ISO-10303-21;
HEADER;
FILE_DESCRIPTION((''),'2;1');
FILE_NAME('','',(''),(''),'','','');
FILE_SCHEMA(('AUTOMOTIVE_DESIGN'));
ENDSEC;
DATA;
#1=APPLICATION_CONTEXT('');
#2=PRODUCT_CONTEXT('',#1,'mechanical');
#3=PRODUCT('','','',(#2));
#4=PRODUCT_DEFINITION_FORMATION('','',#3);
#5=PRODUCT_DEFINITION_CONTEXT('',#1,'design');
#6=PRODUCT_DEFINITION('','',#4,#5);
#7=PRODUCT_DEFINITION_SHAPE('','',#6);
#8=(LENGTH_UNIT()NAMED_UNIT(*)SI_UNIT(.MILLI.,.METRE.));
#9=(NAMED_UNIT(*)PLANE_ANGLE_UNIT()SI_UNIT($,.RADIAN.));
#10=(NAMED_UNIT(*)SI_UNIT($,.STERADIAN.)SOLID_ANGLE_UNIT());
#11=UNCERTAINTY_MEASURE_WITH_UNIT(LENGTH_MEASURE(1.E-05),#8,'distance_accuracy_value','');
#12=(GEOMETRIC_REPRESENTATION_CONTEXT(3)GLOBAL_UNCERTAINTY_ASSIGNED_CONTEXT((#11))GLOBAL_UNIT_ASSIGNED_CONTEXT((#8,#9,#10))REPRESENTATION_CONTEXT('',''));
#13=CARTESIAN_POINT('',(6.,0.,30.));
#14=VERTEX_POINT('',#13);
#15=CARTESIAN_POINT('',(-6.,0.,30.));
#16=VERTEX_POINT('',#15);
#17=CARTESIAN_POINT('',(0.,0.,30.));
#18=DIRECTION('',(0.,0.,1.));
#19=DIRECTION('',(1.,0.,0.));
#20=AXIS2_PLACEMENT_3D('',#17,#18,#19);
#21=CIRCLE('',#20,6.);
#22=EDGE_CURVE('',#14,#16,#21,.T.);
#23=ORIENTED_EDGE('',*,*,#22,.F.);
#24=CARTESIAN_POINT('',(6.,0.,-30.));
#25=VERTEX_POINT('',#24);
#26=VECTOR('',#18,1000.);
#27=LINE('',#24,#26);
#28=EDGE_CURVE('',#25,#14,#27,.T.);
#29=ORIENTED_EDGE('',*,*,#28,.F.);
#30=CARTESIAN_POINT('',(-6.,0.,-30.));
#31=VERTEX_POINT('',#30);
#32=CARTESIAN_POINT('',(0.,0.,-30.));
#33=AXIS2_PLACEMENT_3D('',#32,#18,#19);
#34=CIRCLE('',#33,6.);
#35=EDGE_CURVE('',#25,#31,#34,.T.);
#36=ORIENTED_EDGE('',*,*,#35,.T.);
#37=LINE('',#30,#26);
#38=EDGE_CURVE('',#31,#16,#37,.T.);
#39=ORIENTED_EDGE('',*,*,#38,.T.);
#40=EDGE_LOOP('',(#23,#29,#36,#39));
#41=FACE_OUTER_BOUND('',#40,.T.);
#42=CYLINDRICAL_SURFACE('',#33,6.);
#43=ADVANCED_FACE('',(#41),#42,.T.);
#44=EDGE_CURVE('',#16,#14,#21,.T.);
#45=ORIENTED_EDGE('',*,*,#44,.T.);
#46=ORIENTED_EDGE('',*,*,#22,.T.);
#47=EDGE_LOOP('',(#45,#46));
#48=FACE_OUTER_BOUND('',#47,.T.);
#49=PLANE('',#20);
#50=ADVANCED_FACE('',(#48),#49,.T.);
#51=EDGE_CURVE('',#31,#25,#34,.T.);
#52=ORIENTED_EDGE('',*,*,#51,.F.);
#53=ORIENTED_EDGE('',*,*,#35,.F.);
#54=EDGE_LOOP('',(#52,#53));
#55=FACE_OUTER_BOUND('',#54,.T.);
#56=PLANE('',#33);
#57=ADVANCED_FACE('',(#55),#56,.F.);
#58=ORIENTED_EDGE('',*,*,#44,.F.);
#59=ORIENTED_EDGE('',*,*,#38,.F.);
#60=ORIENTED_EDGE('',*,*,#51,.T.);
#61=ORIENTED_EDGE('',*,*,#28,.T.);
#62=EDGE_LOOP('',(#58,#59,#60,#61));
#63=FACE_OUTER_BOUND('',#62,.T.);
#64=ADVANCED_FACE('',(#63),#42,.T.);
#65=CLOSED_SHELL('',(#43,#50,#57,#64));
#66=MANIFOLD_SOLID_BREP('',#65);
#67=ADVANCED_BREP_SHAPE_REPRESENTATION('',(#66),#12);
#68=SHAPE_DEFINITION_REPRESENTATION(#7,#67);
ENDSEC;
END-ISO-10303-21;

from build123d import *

# Parameters (mm, degrees)
SKETCH_1_R      = 6
EXTRUDE_1_DEPTH = 30


with BuildPart() as part:
    # 草图1 → 凸台-拉伸1 (new, symmetric)
    with BuildSketch(Plane.XY):
        Circle(SKETCH_1_R)
    extrude(amount=EXTRUDE_1_DEPTH, both=True)


solid = part.part
